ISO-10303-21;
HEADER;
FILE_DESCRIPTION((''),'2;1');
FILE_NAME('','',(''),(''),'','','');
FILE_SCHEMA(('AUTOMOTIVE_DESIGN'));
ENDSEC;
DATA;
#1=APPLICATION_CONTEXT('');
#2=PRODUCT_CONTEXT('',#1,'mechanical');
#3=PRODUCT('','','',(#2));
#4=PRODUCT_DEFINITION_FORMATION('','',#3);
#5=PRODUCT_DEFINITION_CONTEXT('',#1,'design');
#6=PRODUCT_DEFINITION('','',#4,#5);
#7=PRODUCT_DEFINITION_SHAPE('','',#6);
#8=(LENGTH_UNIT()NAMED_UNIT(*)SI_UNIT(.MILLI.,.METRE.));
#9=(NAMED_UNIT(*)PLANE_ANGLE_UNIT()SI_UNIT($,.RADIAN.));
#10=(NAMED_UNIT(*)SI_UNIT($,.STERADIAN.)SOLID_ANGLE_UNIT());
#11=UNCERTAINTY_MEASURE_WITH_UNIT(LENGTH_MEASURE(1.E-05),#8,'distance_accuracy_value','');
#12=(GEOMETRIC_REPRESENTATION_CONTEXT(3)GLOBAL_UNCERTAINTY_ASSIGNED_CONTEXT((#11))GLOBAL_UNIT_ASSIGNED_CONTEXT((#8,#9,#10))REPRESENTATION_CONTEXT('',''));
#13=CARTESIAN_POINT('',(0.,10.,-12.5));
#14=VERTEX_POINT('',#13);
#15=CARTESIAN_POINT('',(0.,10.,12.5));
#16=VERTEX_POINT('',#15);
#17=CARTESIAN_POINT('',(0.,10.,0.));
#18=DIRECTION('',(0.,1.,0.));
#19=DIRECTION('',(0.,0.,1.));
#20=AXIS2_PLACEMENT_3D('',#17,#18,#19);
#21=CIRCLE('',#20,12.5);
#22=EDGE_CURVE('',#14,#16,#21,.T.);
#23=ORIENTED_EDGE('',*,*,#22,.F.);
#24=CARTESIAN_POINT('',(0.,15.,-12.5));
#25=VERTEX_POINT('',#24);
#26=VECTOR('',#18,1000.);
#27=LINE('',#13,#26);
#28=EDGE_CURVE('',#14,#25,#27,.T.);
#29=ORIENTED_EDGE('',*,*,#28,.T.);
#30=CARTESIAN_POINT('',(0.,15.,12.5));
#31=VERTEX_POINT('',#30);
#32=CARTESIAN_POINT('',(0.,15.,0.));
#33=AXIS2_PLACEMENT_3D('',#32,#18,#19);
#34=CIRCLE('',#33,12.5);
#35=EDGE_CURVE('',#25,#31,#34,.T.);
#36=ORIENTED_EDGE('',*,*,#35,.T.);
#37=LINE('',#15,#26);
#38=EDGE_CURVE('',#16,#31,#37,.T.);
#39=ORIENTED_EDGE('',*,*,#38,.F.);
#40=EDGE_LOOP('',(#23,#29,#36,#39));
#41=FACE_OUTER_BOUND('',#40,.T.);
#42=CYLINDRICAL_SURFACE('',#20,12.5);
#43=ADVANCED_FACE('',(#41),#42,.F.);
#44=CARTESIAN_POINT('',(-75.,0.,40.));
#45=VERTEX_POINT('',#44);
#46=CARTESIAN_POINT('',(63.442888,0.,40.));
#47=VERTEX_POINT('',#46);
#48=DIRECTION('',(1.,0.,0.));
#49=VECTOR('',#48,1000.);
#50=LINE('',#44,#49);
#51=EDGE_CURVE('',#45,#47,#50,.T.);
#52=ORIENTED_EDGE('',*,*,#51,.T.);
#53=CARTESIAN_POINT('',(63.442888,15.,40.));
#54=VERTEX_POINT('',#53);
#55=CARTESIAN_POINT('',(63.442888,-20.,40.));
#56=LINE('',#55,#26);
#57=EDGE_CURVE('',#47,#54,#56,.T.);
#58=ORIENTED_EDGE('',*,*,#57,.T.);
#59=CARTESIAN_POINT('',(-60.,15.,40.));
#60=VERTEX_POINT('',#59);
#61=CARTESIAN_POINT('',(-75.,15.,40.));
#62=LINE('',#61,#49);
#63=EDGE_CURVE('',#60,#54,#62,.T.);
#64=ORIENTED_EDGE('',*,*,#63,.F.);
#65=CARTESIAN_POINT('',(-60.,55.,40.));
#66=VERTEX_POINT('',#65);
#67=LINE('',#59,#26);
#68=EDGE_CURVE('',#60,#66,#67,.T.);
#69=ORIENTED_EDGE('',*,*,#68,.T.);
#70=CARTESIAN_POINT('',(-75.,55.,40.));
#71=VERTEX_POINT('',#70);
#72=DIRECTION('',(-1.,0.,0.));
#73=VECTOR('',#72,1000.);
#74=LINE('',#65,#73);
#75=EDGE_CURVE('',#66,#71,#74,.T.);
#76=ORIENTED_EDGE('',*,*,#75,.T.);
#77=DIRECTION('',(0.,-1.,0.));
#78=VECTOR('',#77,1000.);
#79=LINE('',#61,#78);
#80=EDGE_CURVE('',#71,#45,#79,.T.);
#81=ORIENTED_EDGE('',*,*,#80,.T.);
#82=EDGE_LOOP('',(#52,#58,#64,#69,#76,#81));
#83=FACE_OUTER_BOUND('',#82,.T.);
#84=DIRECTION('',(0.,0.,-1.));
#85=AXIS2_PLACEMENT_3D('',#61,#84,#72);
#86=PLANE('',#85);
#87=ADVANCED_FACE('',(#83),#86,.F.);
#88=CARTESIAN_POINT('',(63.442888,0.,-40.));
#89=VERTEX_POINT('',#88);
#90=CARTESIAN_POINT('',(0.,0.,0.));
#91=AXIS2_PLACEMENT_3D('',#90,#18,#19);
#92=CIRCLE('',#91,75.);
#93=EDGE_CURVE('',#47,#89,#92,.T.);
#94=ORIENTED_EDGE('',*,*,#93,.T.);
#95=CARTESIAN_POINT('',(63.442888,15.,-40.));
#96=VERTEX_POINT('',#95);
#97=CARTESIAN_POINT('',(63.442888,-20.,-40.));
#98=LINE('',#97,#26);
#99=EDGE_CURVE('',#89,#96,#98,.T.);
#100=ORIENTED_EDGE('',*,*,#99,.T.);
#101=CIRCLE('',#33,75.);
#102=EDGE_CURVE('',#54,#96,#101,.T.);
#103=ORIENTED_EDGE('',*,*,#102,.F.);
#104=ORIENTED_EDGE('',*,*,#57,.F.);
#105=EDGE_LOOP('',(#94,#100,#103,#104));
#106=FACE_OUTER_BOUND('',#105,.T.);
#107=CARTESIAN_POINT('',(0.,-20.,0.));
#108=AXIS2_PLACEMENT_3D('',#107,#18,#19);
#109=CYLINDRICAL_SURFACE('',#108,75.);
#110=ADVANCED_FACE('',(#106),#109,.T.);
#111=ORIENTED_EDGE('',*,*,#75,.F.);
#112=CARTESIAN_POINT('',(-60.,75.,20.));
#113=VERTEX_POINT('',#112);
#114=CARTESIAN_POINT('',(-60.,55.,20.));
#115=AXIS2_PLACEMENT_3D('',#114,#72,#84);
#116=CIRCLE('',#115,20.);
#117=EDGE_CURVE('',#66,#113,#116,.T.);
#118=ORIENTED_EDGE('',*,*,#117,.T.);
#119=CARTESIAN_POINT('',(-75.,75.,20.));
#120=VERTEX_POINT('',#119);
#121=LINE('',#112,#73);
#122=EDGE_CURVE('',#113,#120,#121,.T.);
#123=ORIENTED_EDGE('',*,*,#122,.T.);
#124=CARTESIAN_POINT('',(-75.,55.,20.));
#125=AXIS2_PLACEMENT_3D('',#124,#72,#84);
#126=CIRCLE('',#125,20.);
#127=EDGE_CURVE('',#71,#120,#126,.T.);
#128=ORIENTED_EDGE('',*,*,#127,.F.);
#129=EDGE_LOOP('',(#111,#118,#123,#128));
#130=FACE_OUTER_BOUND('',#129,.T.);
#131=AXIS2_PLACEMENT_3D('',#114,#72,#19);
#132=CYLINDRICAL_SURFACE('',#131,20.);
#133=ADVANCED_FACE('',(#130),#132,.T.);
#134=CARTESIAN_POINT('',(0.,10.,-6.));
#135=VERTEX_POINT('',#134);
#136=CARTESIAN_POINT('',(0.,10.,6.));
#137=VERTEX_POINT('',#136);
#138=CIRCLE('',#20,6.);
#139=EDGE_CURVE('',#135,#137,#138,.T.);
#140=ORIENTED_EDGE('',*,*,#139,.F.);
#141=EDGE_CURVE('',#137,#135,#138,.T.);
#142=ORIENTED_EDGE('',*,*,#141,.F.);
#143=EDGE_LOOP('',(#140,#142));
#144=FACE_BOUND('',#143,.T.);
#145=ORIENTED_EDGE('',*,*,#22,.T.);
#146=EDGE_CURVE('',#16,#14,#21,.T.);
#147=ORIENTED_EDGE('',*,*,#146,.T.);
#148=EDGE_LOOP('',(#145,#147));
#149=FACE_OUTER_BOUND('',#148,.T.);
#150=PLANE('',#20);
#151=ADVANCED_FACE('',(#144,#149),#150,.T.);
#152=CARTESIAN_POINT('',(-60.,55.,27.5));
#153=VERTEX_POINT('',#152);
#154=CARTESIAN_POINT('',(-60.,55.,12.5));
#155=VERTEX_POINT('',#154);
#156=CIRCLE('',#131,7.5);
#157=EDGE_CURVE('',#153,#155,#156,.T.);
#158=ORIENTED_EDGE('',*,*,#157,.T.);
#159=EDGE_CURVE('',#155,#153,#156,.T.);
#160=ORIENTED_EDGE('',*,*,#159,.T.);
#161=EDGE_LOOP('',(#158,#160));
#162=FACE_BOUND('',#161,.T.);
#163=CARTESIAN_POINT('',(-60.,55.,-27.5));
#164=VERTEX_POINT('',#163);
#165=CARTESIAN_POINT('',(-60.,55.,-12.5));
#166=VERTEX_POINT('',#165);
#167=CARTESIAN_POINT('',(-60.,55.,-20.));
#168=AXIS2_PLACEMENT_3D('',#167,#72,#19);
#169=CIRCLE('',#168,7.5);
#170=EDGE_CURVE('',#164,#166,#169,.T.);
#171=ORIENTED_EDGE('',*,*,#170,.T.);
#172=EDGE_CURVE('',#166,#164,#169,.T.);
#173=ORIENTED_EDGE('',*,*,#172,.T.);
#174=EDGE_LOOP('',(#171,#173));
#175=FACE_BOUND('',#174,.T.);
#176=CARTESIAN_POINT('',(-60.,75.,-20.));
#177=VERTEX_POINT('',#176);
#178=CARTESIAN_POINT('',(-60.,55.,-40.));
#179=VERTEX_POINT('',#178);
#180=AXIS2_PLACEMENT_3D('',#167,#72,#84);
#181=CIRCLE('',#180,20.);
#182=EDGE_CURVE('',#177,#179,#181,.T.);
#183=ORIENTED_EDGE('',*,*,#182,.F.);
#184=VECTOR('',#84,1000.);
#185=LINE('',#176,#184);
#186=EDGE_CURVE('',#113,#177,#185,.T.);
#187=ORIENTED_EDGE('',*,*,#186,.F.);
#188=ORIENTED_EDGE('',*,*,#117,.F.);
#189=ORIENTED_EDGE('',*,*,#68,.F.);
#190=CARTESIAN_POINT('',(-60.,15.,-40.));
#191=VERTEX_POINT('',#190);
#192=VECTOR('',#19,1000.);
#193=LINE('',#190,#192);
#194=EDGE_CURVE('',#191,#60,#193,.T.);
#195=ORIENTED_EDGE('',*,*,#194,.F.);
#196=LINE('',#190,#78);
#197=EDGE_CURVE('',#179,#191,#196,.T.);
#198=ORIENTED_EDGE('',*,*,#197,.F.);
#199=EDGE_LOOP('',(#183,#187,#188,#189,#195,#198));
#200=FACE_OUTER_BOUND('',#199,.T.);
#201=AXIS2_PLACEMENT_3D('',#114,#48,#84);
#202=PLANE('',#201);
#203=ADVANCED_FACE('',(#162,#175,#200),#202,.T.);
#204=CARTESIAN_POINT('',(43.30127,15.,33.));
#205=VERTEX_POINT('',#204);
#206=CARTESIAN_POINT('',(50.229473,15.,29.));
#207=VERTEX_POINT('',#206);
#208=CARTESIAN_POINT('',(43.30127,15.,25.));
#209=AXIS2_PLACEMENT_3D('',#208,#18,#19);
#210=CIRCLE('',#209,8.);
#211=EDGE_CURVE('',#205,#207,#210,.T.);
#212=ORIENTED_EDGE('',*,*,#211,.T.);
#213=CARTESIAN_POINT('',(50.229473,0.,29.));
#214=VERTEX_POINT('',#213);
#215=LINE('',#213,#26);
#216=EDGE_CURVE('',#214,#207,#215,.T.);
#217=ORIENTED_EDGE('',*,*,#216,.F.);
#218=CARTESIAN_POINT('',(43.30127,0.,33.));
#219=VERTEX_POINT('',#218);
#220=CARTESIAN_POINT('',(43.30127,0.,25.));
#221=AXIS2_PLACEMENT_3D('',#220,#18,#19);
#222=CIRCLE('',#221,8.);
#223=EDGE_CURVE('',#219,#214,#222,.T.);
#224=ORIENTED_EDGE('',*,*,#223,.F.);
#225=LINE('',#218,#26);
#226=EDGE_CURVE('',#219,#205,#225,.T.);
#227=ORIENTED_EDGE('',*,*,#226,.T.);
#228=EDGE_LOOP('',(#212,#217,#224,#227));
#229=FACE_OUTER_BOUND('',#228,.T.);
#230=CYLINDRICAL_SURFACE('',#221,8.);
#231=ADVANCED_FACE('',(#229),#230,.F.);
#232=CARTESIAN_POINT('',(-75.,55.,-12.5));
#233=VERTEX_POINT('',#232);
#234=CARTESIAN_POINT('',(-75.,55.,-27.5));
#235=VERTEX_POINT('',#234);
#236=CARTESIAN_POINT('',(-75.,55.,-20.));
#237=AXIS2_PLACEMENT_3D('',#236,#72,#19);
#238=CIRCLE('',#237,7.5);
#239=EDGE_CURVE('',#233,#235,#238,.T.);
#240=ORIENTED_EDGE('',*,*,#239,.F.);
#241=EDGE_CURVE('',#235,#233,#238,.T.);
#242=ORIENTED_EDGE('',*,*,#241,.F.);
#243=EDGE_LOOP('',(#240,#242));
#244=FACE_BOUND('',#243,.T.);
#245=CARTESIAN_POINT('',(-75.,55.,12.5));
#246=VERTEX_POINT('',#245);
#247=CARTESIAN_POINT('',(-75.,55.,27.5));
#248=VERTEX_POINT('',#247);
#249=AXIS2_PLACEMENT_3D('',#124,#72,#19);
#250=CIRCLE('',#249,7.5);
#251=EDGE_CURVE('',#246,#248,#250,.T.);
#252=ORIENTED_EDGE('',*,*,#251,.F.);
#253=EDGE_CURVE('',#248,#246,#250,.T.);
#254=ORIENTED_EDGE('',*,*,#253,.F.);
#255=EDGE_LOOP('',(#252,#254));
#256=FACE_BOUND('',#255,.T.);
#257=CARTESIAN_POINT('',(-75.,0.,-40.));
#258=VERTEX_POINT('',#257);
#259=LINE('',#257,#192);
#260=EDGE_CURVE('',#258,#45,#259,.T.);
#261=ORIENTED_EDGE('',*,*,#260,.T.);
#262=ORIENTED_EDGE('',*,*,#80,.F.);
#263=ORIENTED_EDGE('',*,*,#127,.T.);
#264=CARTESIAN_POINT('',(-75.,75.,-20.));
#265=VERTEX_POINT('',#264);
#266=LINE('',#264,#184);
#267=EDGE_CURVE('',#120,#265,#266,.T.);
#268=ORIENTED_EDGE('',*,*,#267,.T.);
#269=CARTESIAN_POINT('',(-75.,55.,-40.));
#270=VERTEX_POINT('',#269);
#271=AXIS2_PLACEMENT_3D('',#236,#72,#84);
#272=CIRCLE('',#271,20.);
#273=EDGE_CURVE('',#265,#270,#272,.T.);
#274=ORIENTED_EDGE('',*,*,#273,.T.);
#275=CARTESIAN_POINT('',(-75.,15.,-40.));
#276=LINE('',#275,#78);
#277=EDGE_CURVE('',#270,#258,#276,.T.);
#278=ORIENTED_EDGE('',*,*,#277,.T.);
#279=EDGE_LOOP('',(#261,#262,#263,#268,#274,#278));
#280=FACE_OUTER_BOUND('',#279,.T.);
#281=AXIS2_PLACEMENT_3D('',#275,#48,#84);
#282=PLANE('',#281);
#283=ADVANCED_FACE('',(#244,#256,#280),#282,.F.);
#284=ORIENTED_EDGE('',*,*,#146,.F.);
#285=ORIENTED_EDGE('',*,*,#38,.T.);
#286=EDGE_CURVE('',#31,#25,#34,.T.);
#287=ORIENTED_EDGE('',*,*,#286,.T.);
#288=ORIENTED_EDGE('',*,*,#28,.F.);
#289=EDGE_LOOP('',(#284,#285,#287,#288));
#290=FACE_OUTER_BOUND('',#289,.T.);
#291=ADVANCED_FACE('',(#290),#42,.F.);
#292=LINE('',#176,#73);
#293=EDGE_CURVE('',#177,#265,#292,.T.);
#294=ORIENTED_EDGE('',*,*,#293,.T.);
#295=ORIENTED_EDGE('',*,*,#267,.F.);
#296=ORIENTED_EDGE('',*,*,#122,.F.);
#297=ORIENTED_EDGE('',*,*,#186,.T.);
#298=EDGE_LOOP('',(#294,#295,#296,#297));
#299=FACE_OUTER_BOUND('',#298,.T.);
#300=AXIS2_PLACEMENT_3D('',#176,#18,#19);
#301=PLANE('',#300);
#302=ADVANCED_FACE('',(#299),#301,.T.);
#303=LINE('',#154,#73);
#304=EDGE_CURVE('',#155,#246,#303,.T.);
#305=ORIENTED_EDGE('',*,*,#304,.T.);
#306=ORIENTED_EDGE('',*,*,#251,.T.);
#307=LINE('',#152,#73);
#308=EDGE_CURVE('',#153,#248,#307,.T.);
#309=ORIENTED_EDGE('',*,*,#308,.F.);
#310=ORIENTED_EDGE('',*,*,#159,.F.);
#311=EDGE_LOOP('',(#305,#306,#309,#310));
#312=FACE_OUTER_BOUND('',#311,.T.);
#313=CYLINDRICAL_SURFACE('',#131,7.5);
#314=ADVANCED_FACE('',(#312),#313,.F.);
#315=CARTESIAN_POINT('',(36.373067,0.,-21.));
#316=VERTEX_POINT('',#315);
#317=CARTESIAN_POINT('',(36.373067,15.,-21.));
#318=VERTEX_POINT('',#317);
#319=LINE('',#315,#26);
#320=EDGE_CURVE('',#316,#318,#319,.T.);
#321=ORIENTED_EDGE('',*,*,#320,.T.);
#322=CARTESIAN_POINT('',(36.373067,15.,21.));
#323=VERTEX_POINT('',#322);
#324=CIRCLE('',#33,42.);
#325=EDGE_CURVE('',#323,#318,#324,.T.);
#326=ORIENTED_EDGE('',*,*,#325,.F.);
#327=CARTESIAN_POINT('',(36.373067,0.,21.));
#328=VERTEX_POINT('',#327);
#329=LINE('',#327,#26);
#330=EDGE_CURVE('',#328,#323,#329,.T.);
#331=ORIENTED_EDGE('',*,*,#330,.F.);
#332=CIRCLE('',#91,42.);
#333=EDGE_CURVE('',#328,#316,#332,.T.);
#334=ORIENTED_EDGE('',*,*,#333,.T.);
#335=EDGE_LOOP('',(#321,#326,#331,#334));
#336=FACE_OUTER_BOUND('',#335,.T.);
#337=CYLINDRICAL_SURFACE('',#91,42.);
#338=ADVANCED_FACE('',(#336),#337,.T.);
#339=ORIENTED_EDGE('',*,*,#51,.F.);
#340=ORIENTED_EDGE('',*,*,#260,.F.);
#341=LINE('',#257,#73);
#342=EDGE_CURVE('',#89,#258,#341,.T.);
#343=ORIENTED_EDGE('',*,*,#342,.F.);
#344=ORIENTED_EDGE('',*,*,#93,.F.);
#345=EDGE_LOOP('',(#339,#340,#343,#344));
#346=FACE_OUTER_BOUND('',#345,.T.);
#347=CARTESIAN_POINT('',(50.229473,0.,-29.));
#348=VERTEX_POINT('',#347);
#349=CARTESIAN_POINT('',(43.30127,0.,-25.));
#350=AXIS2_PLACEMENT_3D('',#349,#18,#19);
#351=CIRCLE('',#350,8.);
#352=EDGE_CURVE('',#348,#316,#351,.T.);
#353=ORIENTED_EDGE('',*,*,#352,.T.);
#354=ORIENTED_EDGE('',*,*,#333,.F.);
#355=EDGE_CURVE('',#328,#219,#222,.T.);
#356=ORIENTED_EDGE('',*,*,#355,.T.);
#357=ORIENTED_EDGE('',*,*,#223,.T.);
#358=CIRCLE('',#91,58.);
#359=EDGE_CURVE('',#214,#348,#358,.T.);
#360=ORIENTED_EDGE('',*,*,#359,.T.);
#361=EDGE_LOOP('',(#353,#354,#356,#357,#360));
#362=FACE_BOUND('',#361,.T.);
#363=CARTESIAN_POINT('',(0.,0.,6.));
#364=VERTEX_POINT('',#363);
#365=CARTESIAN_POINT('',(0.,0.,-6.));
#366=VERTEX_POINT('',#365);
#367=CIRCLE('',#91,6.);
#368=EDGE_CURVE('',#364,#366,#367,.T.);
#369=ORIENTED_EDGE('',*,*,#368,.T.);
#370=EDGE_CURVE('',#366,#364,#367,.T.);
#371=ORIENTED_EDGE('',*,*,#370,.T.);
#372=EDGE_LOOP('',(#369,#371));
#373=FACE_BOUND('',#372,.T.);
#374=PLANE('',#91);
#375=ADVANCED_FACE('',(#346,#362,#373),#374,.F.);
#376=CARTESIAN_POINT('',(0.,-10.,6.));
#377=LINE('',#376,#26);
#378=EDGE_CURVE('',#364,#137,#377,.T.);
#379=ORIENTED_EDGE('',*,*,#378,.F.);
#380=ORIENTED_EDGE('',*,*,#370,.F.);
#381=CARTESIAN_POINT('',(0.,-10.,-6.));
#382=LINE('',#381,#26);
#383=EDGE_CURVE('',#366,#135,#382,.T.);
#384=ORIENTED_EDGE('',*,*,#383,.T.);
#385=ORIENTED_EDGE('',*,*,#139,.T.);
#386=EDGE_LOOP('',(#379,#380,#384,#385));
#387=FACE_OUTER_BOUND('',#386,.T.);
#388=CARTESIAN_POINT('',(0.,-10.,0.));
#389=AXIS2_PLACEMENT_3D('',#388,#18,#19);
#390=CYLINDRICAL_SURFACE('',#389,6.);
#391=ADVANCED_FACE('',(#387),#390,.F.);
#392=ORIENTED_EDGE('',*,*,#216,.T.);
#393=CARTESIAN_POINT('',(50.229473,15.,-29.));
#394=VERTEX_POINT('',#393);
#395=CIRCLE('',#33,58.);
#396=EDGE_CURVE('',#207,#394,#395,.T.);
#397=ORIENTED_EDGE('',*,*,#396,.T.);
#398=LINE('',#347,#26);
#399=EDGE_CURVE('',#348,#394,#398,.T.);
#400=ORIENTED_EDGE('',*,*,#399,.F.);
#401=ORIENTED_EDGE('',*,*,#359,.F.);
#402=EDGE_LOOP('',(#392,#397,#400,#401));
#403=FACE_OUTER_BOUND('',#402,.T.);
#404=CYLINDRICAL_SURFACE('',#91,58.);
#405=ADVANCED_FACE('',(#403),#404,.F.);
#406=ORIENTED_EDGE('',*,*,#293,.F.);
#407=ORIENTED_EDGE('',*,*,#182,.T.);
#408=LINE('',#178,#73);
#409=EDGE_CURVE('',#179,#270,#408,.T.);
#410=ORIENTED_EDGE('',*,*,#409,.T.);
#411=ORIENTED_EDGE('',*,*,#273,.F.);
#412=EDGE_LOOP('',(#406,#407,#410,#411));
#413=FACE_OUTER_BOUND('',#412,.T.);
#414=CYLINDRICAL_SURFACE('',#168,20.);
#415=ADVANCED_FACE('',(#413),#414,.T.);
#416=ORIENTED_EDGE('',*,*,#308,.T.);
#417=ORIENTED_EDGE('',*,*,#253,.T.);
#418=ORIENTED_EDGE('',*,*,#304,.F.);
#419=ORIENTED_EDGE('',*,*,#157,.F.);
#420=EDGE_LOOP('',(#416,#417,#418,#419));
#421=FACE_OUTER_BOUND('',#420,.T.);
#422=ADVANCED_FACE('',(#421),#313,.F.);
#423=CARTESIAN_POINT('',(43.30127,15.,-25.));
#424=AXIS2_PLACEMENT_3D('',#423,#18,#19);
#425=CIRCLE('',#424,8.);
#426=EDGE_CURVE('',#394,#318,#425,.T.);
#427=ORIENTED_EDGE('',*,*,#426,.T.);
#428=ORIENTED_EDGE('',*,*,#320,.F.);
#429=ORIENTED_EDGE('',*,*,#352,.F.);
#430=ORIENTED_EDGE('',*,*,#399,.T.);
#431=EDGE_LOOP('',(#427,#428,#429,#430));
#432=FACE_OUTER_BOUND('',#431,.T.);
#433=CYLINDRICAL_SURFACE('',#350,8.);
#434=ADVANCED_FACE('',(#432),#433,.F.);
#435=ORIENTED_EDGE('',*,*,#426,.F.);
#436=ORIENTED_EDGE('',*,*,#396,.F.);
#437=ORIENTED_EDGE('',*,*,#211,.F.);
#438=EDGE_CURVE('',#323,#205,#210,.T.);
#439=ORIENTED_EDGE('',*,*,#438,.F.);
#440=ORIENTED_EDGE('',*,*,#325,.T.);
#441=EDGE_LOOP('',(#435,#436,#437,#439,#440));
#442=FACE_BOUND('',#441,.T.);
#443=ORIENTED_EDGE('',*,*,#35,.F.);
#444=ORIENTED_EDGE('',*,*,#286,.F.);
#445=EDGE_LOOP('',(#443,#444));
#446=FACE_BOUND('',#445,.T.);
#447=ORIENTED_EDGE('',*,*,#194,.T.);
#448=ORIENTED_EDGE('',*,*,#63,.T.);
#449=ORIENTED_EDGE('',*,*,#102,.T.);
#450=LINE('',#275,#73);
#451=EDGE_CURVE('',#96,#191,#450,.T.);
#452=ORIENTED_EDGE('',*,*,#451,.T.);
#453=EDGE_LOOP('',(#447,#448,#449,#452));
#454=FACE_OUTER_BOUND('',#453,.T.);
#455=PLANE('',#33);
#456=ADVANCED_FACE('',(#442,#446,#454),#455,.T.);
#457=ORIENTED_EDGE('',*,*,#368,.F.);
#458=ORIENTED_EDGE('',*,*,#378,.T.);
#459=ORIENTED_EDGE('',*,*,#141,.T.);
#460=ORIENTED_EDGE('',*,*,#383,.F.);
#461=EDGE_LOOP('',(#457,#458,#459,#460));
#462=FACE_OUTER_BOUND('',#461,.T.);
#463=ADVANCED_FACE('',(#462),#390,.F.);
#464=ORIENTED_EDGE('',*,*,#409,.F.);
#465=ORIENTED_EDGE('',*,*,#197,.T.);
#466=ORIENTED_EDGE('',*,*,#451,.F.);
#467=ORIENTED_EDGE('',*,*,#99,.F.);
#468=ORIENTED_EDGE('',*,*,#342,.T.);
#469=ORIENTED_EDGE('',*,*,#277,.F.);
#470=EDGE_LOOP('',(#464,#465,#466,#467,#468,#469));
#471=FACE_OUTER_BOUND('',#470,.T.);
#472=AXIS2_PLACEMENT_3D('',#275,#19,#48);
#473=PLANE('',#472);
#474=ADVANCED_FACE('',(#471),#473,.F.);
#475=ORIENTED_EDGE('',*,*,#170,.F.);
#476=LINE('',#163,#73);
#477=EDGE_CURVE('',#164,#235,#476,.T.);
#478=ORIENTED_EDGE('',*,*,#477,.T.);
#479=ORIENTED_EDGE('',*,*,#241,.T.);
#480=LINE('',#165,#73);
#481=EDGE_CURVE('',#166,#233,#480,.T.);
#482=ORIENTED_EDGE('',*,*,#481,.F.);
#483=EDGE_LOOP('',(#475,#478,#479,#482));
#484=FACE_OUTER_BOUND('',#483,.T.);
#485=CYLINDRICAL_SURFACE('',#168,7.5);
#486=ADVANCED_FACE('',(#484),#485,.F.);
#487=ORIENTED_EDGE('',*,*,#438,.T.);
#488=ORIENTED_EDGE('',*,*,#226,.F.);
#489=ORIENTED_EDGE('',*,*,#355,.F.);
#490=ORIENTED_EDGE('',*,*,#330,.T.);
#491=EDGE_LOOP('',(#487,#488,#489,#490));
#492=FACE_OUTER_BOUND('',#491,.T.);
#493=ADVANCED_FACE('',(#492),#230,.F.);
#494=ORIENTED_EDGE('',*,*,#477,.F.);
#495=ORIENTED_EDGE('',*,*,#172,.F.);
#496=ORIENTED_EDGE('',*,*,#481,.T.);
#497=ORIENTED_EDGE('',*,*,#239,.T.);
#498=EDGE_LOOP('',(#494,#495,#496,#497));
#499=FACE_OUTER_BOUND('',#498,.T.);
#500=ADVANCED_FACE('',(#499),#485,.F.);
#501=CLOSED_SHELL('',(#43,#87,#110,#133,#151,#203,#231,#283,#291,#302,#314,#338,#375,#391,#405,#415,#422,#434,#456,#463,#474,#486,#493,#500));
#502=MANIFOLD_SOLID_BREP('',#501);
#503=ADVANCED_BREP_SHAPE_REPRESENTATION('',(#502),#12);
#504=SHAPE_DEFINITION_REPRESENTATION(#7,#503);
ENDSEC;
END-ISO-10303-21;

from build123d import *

# Parameters (mm, degrees)
BASE_PLATE_SKETCH_W             = 150
BASE_PLATE_SKETCH_H             = 80
BASE_PLATE_DEPTH                = 15
PROFILE_TRIM_CUT_DEPTH          = 35
COUNTERBORE_SKETCH_R            = 12.5
COUNTERBORE_SKETCH_R_2          = 6
COUNTERBORE_25X5_DEPTH          = 5
THROUGH_HOLE_SKETCH_R           = 6
THROUGH_HOLE_CUT_DEPTH          = 25
ARC_SLOT_8_R50_30DEG_DEPTH      = 86.586213843
ARC_SLOT_8_R50_30DEG_DEPTH_BACK = 86.586213843
UPRIGHT_FLANGE_SKETCH_R         = 7.5
UPRIGHT_FLANGE_DEPTH            = 15


with BuildPart() as part:
    # Base Plate Sketch → Base Plate (new body)
    with BuildSketch(Plane(origin=(0, 0, 0), x_dir=(1, 0, 0), z_dir=(0, 1, 0))):
        Rectangle(BASE_PLATE_SKETCH_W, BASE_PLATE_SKETCH_H)
    extrude(amount=BASE_PLATE_DEPTH)

    # Profile Trim Sketch → Profile Trim Cut (cut)
    with BuildSketch(Plane(origin=(0, 15, 0), x_dir=(1, 0, 0), z_dir=(0, 1, 0))):
        with BuildLine():
            Line((75, 0), (75, 40))
            Line((75, 40), (63.442887702, 40))
            ThreePointArc((63.442887702, 40), (72.052815967, 20.818062138), (75, 0))
        make_face()
        with BuildLine():
            Line((75, -40), (75, 0))
            ThreePointArc((75, 0), (72.052815967, -20.818062138), (63.442887702, -40))
            Line((63.442887702, -40), (75, -40))
        make_face()
    extrude(amount=-PROFILE_TRIM_CUT_DEPTH, mode=Mode.SUBTRACT)

    # Counterbore Sketch → Counterbore Ø25x5 (cut)
    with BuildSketch(Plane(origin=(0, 15, 0), x_dir=(1, 0, 0), z_dir=(0, 1, 0))):
        with Locations(Location((0, 0, 0), (0, 0, 270))):
            Circle(COUNTERBORE_SKETCH_R)
        with Locations(Location((0, 0, 0), (0, 0, 270))):
            Circle(COUNTERBORE_SKETCH_R_2, mode=Mode.SUBTRACT)
    extrude(amount=-COUNTERBORE_25X5_DEPTH, mode=Mode.SUBTRACT)

    # Through Hole Sketch → Through Hole Cut (cut)
    with BuildSketch(Plane(origin=(0, 15, 0), x_dir=(1, 0, 0), z_dir=(0, 1, 0))):
        with Locations(Location((0, 0, 0), (0, 0, 270))):
            Circle(THROUGH_HOLE_SKETCH_R)
    extrude(amount=-THROUGH_HOLE_CUT_DEPTH, mode=Mode.SUBTRACT)

    # Arc Slot Sketch → Arc Slot 8 R50 30deg (cut, two sides: drawn at the far end of the back side and taken through both)
    with BuildSketch(Plane(origin=(0, 10, 0), x_dir=(1, 0, 0), z_dir=(0, 1, 0)).offset(-ARC_SLOT_8_R50_30DEG_DEPTH_BACK)):
        with BuildLine():
            ThreePointArc((50.229473419, -29), (58, 0), (50.229473419, 29))
            ThreePointArc((50.229473419, 29), (39.301270189, 31.92820323), (36.373066959, 21))
            ThreePointArc((36.373066959, 21), (42, 0), (36.373066959, -21))
            ThreePointArc((36.373066959, -21), (39.301270189, -31.92820323), (50.229473419, -29))
        make_face()
    extrude(amount=ARC_SLOT_8_R50_30DEG_DEPTH + ARC_SLOT_8_R50_30DEG_DEPTH_BACK, mode=Mode.SUBTRACT)

    # Upright Flange Sketch → Upright Flange (add)
    with BuildSketch(Plane.ZY.offset(75)):
        with BuildLine():
            Line((-40, 15), (-40, 55))
            ThreePointArc((-40, 55), (-34.142135624, 69.142135624), (-20, 75))
            Line((-20, 75), (20, 75))
            ThreePointArc((20, 75), (34.142135624, 69.142135624), (40, 55))
            Line((40, 55), (40, 15))
            Line((40, 15), (-40, 15))
        make_face()
        with Locations((-20, 55)):
            Circle(UPRIGHT_FLANGE_SKETCH_R, mode=Mode.SUBTRACT)
        with Locations((20, 55)):
            Circle(UPRIGHT_FLANGE_SKETCH_R, mode=Mode.SUBTRACT)
    extrude(amount=-UPRIGHT_FLANGE_DEPTH)


solid = part.part
